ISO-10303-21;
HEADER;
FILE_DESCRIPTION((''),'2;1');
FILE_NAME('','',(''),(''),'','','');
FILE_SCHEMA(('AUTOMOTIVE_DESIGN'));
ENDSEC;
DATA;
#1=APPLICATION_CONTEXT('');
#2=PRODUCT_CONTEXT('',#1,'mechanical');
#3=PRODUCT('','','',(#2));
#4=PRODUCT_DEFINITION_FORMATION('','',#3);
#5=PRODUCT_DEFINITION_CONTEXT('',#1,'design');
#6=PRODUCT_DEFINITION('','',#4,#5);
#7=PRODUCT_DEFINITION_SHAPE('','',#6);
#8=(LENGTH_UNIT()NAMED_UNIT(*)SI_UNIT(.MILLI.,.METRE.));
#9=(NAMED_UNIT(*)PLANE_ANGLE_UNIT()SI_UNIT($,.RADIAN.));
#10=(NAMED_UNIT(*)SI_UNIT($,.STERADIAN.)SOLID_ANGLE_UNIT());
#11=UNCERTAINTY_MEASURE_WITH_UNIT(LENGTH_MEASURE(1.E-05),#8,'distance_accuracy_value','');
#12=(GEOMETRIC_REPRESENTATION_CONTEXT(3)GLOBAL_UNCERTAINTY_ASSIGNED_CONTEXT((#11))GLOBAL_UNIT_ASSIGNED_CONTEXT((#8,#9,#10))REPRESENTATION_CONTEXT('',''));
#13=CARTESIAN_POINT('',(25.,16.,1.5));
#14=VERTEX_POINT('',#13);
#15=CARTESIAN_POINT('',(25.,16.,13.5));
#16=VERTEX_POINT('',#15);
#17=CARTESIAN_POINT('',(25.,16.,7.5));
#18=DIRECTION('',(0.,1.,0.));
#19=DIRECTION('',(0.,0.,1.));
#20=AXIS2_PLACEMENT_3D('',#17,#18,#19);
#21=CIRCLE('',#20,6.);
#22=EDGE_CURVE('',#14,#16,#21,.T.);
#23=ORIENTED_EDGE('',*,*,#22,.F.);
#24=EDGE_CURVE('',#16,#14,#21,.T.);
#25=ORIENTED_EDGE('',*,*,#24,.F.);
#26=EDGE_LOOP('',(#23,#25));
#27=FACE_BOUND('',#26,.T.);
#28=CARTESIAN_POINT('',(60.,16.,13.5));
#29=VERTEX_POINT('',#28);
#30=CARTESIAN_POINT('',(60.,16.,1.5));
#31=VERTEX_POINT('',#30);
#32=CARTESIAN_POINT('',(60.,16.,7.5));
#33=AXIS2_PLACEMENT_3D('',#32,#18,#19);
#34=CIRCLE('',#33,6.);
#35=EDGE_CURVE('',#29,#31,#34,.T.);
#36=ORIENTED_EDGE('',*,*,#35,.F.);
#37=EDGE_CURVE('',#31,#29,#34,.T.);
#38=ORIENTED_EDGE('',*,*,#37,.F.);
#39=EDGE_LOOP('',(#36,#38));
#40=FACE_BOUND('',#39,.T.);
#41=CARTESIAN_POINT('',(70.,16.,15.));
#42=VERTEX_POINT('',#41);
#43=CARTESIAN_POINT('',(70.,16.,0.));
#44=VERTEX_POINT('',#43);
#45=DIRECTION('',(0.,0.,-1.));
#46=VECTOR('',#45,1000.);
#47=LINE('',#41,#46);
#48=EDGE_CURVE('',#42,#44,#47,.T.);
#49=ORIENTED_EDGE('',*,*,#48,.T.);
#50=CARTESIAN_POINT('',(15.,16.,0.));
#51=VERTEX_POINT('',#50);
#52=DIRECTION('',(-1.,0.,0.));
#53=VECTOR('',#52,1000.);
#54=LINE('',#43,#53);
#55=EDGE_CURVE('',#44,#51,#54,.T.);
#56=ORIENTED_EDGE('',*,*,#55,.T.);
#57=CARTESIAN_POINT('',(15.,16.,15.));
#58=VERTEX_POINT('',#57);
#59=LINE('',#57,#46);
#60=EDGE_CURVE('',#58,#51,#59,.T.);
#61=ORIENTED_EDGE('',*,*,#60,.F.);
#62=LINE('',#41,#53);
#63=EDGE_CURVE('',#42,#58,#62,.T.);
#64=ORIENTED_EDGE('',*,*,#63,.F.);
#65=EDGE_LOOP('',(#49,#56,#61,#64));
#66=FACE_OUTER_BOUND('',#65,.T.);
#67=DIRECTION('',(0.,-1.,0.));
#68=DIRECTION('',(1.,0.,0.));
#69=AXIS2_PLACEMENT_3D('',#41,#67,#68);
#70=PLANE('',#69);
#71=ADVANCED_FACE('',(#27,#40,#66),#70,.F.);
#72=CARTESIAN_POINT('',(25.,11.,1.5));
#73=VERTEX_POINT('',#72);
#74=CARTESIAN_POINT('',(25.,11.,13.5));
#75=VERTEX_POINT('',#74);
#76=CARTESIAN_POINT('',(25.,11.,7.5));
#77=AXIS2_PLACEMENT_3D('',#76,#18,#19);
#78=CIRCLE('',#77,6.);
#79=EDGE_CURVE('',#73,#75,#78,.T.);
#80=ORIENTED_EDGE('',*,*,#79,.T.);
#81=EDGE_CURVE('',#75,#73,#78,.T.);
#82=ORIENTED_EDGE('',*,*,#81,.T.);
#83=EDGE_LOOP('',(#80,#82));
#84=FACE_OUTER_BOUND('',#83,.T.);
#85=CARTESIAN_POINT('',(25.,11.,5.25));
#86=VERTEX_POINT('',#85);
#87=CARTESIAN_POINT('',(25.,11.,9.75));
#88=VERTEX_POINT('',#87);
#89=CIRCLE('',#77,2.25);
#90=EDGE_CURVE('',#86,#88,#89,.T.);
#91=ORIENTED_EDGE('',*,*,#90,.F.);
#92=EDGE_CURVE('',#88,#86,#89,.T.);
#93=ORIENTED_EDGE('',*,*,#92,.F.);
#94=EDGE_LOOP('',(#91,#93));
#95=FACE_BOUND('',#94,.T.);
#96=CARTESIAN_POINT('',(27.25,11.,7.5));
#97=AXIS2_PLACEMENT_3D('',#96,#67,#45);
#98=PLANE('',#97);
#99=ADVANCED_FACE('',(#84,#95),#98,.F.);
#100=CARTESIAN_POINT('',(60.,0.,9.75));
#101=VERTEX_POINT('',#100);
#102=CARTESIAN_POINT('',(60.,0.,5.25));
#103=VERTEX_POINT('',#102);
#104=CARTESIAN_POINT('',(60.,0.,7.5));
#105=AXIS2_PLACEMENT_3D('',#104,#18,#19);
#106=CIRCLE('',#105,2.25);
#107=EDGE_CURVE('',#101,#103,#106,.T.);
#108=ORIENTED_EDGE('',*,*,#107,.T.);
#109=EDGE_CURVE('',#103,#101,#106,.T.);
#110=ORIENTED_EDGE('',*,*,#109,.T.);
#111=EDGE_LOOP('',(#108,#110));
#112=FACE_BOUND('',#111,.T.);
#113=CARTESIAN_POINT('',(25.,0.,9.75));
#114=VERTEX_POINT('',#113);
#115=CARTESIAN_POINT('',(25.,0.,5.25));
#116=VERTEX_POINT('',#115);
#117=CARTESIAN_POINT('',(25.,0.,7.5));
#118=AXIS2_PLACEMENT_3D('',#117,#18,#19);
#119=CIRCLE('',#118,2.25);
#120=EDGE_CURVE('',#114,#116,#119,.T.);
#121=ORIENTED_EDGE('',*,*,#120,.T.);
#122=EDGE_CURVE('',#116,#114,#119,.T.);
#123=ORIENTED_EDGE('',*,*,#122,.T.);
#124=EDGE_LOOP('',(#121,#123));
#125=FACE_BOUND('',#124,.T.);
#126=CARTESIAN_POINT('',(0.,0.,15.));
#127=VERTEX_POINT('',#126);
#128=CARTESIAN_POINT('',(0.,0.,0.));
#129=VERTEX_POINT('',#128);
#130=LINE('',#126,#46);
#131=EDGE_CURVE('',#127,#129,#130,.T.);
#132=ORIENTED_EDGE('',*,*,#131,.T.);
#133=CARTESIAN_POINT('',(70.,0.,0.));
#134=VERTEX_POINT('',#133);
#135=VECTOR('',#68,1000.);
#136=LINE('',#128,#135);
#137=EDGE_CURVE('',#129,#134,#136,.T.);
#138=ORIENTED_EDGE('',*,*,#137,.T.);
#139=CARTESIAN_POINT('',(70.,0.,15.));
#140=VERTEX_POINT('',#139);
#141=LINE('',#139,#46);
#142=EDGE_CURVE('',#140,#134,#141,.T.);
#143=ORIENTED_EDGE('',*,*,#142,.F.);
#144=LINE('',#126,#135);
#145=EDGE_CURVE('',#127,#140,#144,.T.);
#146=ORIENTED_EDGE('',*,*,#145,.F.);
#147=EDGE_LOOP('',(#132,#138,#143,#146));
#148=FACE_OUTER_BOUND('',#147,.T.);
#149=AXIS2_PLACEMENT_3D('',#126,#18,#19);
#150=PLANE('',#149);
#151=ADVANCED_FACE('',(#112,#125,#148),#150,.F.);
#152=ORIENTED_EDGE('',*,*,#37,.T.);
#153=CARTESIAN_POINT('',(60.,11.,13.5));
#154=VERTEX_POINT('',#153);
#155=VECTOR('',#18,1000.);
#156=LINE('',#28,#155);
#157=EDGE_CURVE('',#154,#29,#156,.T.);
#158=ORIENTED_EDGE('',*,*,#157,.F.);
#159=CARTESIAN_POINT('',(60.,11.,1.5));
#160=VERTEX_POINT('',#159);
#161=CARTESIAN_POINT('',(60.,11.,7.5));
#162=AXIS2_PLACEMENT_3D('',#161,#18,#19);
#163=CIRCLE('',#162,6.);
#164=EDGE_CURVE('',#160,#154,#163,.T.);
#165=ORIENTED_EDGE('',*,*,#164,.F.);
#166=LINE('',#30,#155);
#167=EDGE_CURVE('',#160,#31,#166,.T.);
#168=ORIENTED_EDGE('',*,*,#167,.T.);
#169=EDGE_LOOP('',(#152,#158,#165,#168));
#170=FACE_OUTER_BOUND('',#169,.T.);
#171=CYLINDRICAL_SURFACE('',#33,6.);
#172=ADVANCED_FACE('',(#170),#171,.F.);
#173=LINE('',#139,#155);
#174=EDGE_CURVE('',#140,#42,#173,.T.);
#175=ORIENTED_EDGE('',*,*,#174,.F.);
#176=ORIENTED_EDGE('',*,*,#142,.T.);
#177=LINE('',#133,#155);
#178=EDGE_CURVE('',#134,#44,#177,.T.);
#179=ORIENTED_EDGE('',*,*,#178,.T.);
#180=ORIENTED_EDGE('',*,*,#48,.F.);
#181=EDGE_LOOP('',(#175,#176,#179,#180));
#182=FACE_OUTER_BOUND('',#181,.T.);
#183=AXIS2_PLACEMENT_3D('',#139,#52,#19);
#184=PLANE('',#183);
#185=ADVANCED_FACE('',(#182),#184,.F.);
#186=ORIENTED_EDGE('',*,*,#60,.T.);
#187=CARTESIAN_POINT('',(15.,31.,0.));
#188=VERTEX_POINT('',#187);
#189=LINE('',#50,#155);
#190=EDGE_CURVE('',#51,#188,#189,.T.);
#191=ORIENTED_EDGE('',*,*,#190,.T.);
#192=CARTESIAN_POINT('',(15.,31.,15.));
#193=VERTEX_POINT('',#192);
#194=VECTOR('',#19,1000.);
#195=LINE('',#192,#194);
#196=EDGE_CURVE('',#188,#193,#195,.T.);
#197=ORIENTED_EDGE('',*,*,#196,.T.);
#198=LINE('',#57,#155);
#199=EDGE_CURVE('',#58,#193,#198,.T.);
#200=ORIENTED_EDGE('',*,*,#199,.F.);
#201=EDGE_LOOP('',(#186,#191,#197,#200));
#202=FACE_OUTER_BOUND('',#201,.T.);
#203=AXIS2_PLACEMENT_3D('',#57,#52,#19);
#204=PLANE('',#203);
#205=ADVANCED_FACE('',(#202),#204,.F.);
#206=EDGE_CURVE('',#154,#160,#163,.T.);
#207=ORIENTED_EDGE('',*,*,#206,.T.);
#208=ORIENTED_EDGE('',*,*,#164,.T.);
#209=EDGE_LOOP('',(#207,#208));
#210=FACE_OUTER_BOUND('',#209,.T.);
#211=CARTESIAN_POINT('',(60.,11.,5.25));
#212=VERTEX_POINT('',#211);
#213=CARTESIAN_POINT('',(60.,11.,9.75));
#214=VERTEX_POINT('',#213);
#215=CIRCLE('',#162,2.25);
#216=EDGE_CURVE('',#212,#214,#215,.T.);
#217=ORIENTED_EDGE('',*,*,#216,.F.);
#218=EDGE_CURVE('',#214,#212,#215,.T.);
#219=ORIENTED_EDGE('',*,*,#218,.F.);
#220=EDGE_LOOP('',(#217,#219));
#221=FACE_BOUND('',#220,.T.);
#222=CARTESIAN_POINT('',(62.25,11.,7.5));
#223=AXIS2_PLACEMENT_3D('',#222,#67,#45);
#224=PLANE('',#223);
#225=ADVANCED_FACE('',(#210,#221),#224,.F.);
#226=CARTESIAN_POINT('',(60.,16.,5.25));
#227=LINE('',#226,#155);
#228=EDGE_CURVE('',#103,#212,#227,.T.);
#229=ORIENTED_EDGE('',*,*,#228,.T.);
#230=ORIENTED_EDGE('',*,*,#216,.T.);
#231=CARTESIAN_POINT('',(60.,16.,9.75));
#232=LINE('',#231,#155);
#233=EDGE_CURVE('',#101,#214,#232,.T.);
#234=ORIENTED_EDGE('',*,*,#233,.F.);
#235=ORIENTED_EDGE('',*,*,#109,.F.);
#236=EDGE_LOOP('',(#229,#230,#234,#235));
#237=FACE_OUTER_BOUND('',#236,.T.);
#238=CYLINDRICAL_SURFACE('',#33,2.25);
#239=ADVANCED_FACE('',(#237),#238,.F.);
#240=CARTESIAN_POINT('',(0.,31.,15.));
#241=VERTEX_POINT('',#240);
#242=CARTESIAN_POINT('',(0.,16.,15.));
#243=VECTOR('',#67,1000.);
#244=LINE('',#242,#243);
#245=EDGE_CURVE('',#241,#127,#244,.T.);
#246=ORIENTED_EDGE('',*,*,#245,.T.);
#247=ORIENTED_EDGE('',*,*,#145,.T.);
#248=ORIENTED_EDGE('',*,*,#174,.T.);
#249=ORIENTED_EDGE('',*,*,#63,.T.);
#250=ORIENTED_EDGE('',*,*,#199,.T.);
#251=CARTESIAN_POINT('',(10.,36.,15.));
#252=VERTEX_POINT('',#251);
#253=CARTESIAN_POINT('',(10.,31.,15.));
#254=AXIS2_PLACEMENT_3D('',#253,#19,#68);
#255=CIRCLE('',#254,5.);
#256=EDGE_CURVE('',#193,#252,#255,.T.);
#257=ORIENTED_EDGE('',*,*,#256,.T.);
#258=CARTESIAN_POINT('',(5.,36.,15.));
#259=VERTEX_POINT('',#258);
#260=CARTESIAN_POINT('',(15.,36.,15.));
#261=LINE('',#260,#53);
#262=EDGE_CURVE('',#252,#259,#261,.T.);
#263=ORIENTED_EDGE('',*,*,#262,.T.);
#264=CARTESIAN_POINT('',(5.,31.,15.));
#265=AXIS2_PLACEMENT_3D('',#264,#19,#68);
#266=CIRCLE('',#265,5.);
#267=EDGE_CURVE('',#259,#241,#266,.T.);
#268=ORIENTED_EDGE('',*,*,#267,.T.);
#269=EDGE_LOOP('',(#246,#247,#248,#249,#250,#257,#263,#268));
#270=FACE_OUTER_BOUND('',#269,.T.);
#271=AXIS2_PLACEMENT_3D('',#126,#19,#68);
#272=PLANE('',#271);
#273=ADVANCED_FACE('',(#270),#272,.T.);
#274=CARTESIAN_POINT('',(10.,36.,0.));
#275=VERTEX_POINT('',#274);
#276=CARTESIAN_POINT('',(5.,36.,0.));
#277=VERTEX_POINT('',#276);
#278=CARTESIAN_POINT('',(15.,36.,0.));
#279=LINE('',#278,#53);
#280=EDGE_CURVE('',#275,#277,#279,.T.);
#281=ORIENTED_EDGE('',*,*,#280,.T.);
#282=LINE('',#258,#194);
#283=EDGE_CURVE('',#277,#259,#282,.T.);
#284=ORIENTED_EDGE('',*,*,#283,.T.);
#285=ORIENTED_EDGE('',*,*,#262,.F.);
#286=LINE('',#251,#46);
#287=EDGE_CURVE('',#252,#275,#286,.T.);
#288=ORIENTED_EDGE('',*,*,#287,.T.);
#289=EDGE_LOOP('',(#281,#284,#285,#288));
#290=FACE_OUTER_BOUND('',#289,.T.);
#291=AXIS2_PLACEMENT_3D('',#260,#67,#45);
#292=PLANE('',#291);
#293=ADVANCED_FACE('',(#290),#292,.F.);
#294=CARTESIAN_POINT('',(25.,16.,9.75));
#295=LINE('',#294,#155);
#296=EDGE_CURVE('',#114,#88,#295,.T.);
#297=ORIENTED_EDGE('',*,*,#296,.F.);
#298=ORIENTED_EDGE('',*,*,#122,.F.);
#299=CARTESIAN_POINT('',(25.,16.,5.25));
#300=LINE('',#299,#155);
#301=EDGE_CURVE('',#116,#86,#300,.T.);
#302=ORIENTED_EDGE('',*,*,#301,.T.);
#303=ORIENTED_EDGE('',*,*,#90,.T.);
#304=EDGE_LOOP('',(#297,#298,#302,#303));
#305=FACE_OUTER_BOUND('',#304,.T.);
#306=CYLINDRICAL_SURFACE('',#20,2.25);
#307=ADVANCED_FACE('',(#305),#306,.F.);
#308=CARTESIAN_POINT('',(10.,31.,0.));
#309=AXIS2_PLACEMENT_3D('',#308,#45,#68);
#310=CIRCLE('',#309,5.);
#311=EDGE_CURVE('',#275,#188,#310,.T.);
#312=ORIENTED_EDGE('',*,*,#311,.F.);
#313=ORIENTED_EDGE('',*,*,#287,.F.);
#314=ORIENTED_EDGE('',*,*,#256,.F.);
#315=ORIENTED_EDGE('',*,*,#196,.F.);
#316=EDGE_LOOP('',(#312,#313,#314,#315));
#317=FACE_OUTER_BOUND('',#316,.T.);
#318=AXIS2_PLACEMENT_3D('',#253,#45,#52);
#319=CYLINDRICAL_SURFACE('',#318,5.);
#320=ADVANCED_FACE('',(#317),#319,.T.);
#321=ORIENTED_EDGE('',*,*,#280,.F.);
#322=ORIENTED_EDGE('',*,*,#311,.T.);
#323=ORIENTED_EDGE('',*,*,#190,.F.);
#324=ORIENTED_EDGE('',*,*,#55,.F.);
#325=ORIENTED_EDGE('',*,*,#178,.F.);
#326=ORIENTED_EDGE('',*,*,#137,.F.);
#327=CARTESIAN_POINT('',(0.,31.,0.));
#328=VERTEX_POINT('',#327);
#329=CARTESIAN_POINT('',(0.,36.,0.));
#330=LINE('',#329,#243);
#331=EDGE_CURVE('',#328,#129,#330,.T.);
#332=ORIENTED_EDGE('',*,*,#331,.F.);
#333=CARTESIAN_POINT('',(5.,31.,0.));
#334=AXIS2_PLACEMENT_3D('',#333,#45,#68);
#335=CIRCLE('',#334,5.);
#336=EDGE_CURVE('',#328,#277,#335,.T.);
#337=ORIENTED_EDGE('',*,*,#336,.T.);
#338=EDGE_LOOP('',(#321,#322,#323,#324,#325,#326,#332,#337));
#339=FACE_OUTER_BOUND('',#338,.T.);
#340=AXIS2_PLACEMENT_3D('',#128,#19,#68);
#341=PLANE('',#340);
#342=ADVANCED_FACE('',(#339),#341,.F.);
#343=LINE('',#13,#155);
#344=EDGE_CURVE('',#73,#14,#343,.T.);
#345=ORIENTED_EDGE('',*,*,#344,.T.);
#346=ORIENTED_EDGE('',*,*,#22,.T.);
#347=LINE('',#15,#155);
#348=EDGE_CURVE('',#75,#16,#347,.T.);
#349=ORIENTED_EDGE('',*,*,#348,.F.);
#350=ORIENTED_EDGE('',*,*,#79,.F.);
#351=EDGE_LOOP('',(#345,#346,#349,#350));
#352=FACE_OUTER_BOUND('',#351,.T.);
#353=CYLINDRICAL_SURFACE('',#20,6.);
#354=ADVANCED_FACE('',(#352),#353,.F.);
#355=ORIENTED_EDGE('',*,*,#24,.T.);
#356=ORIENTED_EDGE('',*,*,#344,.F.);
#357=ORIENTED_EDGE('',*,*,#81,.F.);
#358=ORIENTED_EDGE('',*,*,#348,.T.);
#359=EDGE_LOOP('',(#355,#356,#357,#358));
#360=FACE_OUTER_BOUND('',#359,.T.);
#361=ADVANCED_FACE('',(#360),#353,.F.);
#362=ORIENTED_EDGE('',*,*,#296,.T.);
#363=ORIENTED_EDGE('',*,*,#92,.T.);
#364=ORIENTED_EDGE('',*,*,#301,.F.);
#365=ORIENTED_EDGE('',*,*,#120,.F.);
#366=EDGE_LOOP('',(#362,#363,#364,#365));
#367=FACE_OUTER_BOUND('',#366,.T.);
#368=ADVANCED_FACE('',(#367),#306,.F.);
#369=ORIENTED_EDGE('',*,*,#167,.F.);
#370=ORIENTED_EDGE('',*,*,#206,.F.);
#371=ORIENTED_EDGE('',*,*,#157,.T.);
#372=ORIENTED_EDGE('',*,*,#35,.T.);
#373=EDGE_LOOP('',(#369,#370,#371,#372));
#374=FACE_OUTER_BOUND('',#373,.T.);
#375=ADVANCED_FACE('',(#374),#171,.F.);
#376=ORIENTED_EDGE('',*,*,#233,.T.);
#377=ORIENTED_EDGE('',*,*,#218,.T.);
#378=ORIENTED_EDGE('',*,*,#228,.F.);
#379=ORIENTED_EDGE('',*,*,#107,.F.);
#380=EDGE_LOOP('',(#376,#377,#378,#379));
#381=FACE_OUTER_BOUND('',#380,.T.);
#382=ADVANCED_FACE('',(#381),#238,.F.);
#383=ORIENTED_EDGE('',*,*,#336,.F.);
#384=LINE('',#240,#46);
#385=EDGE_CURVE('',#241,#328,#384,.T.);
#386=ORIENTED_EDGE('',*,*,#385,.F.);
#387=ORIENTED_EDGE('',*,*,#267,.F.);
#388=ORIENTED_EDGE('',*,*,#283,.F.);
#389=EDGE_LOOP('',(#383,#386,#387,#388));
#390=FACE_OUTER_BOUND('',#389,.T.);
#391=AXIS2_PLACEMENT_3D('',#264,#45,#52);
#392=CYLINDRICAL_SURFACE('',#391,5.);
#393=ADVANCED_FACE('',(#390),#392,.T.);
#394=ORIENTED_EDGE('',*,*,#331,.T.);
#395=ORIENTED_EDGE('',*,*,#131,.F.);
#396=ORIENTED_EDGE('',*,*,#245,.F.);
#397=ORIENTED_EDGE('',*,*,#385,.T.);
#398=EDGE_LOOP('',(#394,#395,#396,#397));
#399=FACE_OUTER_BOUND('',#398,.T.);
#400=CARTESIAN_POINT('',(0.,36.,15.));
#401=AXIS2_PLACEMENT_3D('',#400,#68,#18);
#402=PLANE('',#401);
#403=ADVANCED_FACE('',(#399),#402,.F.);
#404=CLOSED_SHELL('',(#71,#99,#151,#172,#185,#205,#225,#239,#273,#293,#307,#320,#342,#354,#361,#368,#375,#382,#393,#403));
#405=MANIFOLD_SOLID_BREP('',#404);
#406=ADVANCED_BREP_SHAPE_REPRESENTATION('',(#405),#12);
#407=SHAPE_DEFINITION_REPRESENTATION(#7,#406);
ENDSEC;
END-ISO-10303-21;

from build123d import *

# Parameters (mm, degrees)
EXTRUDE_1_DEPTH           = 15
FILLET_1_R                = 5
HOLE_WIZARD_1_D           = 4.5
HOLE_WIZARD_1_DEPTH       = 100
HOLE_WIZARD_1_CBORE_D     = 12
HOLE_WIZARD_1_CBORE_DEPTH = 5


with BuildPart() as part:
    # 草图1 → 凸台-拉伸1 (new body)
    with BuildSketch(Plane.XY):
        Polygon((0, 0), (70, 0), (70, 16), (15, 16), (15, 36), (0, 36), (0, 16), align=None)
    extrude(amount=EXTRUDE_1_DEPTH)

    # 圆角1
    fillet_1_edges = [part.edges().sort_by_distance(p)[0] for p in [
        (0, 36, 7.5),
        (15, 36, 7.5),
    ]]
    fillet(fillet_1_edges, radius=FILLET_1_R)

    # 孔1
    with Locations(Plane(origin=(0, 16, 0), x_dir=(-1, 0, 0), z_dir=(0, 1, 0))):
        with Locations((-25, 7.5), (-60, 7.5)):
            CounterBoreHole(HOLE_WIZARD_1_D / 2, HOLE_WIZARD_1_CBORE_D / 2, HOLE_WIZARD_1_CBORE_DEPTH, depth=HOLE_WIZARD_1_DEPTH)


solid = part.part
